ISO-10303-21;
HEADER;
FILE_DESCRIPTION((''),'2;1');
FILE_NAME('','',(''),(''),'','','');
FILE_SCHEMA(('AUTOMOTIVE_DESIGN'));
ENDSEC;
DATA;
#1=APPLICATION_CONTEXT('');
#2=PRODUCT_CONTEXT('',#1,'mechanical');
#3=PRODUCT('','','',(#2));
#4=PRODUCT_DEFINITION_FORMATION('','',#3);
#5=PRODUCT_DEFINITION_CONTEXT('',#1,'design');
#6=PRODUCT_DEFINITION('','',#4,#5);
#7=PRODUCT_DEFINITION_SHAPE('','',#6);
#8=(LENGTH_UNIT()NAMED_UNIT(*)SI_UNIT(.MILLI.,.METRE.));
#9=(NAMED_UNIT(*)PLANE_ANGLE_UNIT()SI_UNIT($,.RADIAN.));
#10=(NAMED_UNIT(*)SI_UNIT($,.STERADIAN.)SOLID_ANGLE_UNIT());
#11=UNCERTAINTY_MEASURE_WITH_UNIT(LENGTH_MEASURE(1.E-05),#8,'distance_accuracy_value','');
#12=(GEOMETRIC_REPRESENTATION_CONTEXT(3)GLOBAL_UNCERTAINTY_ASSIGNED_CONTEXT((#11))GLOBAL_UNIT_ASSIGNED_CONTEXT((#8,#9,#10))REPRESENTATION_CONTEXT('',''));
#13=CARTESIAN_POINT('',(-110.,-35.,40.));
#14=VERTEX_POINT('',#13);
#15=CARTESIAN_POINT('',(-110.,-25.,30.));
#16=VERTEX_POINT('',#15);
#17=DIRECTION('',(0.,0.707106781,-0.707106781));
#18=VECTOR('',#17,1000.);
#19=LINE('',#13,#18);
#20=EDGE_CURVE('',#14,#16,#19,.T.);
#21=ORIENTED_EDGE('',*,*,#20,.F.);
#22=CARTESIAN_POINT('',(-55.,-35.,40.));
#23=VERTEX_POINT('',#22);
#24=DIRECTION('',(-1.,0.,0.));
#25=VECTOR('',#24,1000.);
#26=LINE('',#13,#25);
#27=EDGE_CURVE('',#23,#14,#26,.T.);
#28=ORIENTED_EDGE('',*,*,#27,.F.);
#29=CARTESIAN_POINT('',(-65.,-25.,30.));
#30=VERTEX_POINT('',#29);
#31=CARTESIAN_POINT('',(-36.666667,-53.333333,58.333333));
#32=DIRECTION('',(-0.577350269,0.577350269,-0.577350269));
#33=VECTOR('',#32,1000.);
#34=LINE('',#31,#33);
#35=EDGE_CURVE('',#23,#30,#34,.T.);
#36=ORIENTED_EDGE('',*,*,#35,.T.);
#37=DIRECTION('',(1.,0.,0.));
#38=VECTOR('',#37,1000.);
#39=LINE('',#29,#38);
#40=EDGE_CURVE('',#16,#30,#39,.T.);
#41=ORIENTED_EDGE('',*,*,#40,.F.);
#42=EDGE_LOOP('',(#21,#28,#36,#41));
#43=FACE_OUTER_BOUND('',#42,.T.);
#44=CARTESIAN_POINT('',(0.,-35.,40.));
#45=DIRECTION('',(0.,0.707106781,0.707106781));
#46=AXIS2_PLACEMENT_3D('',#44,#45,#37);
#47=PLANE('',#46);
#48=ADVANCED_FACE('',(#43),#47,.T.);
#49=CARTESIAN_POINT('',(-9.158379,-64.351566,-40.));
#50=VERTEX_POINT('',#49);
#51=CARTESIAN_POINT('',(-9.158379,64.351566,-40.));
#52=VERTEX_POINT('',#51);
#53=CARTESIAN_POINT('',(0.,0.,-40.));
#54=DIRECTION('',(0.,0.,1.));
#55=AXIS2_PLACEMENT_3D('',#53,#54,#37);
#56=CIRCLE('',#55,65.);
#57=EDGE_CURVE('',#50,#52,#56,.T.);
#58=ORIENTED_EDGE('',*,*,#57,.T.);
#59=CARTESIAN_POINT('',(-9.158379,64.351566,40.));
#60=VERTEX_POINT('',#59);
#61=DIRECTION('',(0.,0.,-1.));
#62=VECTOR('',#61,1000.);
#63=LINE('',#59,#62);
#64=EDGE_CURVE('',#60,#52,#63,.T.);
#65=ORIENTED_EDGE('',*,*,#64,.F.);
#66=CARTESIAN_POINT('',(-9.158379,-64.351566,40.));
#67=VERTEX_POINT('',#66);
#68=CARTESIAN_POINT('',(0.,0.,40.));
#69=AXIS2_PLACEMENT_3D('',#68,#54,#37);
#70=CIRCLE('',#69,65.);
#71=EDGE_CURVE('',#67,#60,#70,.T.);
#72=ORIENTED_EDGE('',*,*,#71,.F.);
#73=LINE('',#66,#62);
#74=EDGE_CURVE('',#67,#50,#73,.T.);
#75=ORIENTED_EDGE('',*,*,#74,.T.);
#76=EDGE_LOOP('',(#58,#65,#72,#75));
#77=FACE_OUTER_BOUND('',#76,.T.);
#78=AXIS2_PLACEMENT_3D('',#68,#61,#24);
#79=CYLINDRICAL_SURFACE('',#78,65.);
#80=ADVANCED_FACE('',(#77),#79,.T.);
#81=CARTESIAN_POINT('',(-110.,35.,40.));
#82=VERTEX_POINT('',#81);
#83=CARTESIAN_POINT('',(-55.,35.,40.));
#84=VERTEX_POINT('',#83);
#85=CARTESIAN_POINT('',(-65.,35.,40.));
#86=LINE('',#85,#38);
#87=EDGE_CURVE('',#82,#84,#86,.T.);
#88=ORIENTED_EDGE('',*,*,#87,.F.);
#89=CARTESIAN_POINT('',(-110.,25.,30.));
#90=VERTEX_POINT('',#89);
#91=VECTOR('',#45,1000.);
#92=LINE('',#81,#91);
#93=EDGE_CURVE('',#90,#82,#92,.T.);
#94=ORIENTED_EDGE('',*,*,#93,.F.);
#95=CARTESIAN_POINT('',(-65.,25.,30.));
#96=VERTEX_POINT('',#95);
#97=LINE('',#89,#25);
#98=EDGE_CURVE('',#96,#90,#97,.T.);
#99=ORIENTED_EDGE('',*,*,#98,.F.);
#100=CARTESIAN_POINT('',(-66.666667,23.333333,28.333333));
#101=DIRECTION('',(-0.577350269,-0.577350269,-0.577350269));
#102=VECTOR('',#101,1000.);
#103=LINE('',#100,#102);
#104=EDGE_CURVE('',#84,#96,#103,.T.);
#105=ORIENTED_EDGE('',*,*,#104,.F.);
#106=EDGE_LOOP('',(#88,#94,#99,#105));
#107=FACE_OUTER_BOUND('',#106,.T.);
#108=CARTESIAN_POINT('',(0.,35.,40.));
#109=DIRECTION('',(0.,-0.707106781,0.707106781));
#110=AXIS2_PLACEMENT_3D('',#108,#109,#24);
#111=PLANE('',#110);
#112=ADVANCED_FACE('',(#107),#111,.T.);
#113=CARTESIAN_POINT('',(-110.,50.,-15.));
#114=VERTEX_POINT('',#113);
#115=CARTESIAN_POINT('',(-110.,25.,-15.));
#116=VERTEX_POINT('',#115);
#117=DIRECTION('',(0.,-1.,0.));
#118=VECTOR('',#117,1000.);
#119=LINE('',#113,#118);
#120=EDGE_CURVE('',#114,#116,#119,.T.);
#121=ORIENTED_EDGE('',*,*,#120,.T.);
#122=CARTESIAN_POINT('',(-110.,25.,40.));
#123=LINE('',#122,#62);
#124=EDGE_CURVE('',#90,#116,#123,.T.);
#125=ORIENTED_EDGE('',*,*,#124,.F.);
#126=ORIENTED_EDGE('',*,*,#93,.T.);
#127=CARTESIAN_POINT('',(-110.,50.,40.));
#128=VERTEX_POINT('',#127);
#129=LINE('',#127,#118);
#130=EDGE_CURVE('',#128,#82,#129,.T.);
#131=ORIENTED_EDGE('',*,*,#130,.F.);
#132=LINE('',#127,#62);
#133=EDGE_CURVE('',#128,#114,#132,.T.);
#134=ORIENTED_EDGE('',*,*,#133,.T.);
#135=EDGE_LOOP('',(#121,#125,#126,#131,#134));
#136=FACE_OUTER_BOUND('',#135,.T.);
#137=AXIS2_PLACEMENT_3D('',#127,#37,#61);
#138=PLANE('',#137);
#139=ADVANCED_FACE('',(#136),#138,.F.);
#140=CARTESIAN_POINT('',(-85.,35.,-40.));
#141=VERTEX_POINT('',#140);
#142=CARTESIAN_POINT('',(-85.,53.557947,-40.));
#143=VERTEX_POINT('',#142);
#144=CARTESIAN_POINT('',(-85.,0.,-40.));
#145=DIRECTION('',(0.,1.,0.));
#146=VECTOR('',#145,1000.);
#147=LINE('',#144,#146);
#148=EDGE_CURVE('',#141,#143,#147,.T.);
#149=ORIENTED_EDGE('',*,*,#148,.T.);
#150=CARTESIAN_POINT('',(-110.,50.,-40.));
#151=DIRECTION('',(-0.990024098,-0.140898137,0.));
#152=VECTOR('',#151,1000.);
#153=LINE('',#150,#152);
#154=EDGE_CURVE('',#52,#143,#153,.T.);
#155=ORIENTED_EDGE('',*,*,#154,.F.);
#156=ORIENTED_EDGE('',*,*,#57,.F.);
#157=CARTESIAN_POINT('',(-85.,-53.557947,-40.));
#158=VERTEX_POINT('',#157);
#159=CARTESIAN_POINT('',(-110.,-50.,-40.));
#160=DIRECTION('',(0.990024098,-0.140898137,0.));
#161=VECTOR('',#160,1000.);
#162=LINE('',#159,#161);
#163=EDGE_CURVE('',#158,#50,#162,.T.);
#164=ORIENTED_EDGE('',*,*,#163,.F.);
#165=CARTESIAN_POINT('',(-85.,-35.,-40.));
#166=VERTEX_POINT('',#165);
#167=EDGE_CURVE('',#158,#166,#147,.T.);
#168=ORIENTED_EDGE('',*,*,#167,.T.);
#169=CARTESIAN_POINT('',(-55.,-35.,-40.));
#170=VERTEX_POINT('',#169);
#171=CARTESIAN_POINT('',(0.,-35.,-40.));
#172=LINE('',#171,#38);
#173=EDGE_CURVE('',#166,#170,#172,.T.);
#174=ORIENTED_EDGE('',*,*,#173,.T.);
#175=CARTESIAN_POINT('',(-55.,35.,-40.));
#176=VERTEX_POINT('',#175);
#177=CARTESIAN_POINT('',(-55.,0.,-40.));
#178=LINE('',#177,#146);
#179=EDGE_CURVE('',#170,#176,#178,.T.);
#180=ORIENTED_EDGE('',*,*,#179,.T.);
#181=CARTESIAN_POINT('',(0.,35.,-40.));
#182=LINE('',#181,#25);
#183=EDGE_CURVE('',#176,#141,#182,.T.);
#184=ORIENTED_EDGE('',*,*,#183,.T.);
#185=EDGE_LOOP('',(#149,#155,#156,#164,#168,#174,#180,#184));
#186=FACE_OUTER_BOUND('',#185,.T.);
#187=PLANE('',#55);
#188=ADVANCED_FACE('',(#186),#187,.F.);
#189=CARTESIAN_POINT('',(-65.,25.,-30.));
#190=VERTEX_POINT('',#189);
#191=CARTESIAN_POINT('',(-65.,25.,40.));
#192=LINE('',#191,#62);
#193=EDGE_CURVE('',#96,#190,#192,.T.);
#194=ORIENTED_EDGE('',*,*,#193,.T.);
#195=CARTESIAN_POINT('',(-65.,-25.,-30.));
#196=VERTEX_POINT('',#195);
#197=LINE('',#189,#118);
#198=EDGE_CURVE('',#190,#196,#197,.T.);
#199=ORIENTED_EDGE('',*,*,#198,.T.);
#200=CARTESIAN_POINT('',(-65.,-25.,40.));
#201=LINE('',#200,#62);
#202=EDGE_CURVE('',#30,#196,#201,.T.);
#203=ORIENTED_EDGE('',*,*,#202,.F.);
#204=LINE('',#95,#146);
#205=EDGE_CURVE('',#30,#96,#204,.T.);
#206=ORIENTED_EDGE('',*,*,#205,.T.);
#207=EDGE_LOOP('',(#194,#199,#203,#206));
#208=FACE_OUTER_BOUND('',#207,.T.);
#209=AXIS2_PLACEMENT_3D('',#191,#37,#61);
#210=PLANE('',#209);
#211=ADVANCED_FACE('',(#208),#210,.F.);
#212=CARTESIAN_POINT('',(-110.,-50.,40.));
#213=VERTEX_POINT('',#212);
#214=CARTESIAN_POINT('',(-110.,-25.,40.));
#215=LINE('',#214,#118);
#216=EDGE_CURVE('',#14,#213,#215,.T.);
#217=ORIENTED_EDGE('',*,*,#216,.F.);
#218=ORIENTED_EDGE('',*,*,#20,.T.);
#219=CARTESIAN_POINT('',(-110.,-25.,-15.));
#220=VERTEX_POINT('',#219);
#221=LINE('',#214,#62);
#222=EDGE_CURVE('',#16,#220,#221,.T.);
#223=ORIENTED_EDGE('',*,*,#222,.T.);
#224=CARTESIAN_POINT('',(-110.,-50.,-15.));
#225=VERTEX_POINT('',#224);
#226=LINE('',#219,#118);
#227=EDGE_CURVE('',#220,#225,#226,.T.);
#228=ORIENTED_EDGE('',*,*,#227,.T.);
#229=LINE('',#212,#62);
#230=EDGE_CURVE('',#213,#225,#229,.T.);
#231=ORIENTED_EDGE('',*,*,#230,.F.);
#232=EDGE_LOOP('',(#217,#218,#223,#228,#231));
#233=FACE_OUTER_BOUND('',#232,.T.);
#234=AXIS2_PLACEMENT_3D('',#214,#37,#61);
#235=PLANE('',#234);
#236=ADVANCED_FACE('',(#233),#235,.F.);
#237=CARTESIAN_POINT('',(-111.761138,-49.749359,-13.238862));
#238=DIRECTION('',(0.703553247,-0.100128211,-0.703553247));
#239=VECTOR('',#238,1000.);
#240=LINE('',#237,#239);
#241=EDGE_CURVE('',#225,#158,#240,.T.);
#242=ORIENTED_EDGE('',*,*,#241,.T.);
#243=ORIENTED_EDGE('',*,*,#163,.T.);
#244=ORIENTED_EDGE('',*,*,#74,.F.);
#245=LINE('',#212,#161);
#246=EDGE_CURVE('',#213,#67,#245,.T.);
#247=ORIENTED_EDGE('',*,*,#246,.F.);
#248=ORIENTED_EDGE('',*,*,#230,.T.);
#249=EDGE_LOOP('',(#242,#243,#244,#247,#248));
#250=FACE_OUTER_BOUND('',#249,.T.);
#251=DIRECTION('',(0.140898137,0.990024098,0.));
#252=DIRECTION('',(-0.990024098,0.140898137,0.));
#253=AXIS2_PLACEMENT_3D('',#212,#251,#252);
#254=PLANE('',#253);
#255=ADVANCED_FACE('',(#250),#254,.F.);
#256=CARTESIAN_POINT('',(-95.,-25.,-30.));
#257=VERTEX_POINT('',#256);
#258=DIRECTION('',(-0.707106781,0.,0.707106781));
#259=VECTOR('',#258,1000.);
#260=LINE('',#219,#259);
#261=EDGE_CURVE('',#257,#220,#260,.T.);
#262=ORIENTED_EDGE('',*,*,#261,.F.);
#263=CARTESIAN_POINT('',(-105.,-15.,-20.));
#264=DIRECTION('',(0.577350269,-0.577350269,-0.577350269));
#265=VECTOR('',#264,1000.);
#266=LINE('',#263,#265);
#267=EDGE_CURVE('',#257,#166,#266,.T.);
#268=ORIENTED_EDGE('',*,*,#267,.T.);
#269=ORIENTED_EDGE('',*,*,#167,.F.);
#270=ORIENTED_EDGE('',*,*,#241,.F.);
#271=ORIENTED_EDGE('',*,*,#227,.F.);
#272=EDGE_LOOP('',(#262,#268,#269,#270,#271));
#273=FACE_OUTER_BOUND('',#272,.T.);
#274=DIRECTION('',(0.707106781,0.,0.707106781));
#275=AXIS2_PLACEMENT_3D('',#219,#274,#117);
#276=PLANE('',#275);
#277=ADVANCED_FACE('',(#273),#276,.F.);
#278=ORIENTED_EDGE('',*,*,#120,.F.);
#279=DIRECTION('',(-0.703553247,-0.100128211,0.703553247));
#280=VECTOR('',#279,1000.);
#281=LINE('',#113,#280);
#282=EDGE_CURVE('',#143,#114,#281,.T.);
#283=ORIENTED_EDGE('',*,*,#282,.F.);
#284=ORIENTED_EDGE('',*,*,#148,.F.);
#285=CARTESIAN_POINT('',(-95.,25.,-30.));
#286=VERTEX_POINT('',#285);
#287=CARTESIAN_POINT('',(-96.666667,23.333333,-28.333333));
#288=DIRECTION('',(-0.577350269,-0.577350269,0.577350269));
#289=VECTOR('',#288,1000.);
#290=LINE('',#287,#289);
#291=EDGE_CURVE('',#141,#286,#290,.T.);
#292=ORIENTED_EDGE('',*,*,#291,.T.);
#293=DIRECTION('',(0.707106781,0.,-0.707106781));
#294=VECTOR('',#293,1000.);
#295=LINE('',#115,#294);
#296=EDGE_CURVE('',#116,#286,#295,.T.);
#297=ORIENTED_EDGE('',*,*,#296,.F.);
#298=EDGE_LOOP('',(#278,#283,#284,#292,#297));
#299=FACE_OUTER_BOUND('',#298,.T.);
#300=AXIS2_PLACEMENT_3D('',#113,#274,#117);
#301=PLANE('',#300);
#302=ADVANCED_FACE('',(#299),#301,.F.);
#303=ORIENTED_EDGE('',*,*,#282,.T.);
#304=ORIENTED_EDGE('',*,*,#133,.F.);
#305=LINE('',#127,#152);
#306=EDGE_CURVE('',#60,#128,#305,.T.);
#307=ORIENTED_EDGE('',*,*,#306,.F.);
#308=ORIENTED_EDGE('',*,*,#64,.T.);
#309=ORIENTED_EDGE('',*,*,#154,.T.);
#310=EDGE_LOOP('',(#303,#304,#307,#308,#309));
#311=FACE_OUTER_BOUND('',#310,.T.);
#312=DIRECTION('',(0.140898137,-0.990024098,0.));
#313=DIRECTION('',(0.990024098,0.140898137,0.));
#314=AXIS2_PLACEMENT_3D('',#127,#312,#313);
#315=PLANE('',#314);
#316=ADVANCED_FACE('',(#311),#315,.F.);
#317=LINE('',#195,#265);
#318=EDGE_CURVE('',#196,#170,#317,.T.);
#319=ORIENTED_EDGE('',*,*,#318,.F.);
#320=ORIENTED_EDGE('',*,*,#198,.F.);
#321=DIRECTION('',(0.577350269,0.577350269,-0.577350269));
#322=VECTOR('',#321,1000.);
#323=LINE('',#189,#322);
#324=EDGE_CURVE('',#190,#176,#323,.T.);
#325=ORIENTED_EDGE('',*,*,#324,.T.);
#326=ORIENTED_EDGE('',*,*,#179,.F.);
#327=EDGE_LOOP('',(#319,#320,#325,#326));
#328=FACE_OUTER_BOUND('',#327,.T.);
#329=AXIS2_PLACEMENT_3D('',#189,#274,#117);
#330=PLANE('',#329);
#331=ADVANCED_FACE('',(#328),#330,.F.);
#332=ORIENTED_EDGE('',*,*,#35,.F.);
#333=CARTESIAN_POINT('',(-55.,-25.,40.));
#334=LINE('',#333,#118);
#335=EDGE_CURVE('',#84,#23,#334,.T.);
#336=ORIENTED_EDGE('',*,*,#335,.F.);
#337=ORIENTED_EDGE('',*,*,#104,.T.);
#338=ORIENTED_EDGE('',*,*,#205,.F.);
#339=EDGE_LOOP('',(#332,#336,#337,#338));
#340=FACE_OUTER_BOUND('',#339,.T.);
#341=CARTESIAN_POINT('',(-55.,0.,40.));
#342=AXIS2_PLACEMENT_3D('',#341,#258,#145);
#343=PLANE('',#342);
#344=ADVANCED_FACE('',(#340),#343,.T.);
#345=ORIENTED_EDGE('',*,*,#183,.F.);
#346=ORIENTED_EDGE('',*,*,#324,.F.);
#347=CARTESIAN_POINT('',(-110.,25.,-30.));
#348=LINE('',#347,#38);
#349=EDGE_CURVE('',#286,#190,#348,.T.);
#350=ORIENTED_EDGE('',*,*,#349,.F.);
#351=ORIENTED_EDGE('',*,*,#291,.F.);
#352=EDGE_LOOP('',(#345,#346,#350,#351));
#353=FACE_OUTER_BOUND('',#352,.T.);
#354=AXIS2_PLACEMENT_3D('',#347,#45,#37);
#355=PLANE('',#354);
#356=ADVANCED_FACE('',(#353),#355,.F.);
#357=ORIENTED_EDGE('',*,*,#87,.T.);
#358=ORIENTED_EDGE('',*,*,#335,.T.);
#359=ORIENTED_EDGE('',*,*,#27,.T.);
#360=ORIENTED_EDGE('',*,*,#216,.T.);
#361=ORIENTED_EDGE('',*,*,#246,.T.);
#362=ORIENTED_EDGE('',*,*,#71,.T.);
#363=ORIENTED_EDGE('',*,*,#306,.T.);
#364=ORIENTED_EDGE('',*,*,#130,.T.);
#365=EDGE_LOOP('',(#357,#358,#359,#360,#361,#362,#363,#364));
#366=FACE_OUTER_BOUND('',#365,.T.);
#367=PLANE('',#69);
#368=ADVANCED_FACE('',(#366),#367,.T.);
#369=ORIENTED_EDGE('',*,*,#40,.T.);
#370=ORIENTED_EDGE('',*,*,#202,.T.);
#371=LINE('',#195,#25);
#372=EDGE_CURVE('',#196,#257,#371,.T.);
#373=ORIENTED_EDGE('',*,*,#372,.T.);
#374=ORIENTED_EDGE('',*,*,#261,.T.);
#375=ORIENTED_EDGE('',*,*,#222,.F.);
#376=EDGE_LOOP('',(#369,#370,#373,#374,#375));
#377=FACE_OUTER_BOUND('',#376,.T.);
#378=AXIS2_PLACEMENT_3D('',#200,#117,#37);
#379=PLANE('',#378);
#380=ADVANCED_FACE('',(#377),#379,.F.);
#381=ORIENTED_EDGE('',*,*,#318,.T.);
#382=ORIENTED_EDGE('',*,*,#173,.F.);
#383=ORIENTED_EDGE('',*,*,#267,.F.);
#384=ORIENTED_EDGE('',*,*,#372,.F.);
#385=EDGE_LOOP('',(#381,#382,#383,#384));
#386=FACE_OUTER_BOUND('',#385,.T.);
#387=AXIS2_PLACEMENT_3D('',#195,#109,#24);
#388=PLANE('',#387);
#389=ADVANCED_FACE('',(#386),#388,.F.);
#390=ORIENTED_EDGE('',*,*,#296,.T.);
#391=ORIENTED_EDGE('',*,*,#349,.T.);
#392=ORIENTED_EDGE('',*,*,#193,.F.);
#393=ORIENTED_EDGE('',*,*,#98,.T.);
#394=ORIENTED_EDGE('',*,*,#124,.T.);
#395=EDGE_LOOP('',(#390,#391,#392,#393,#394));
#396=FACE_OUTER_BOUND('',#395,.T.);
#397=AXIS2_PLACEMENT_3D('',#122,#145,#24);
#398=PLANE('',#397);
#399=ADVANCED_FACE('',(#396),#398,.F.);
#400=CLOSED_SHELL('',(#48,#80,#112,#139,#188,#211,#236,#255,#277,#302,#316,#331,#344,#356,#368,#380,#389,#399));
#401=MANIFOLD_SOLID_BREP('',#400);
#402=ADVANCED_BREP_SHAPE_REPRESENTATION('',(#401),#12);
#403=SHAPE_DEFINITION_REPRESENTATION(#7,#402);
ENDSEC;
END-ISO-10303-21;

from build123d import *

# Parameters (mm, degrees)
EXTRUDE_1_DEPTH = 40
CHAMFER_1_SIZE  = 25
CHAMFER_2_SIZE  = 10
CHAMFER_3_SIZE  = 10


with BuildPart() as part:
    # 草图1 → 凸台-拉伸1 (new, symmetric)
    with BuildSketch(Plane.XY):
        with BuildLine():
            Line((-110, 50), (-110, 25))
            Line((-110, 25), (-65, 25))
            Line((-65, 25), (-65, -25))
            Line((-65, -25), (-110, -25))
            Line((-110, -25), (-110, -50))
            Line((-110, -50), (-9.158378918, -64.35156638))
            ThreePointArc((-9.158378918, -64.35156638), (65, 0), (-9.158378918, 64.35156638))
            Line((-9.158378918, 64.35156638), (-110, 50))
        make_face()
    extrude(amount=EXTRUDE_1_DEPTH, both=True)

    # 倒角1
    chamfer_1_edges = [part.edges().sort_by_distance(p)[0] for p in [
        (-110, 37.5, -40),
        (-110, -37.5, -40),
    ]]
    chamfer(chamfer_1_edges, length=CHAMFER_1_SIZE)

    # 倒角2
    chamfer_2_edges = [part.edges().sort_by_distance(p)[0] for p in [
        (-87.5, 25, 40),
        (-65, 0, 40),
        (-87.5, -25, 40),
    ]]
    chamfer(chamfer_2_edges, length=CHAMFER_2_SIZE)

    # 倒角3
    chamfer_3_edges = [part.edges().sort_by_distance(p)[0] for p in [
        (-75, 25, -40),
        (-75, -25, -40),
        (-65, 0, -40),
    ]]
    chamfer(chamfer_3_edges, length=CHAMFER_3_SIZE)


solid = part.part
